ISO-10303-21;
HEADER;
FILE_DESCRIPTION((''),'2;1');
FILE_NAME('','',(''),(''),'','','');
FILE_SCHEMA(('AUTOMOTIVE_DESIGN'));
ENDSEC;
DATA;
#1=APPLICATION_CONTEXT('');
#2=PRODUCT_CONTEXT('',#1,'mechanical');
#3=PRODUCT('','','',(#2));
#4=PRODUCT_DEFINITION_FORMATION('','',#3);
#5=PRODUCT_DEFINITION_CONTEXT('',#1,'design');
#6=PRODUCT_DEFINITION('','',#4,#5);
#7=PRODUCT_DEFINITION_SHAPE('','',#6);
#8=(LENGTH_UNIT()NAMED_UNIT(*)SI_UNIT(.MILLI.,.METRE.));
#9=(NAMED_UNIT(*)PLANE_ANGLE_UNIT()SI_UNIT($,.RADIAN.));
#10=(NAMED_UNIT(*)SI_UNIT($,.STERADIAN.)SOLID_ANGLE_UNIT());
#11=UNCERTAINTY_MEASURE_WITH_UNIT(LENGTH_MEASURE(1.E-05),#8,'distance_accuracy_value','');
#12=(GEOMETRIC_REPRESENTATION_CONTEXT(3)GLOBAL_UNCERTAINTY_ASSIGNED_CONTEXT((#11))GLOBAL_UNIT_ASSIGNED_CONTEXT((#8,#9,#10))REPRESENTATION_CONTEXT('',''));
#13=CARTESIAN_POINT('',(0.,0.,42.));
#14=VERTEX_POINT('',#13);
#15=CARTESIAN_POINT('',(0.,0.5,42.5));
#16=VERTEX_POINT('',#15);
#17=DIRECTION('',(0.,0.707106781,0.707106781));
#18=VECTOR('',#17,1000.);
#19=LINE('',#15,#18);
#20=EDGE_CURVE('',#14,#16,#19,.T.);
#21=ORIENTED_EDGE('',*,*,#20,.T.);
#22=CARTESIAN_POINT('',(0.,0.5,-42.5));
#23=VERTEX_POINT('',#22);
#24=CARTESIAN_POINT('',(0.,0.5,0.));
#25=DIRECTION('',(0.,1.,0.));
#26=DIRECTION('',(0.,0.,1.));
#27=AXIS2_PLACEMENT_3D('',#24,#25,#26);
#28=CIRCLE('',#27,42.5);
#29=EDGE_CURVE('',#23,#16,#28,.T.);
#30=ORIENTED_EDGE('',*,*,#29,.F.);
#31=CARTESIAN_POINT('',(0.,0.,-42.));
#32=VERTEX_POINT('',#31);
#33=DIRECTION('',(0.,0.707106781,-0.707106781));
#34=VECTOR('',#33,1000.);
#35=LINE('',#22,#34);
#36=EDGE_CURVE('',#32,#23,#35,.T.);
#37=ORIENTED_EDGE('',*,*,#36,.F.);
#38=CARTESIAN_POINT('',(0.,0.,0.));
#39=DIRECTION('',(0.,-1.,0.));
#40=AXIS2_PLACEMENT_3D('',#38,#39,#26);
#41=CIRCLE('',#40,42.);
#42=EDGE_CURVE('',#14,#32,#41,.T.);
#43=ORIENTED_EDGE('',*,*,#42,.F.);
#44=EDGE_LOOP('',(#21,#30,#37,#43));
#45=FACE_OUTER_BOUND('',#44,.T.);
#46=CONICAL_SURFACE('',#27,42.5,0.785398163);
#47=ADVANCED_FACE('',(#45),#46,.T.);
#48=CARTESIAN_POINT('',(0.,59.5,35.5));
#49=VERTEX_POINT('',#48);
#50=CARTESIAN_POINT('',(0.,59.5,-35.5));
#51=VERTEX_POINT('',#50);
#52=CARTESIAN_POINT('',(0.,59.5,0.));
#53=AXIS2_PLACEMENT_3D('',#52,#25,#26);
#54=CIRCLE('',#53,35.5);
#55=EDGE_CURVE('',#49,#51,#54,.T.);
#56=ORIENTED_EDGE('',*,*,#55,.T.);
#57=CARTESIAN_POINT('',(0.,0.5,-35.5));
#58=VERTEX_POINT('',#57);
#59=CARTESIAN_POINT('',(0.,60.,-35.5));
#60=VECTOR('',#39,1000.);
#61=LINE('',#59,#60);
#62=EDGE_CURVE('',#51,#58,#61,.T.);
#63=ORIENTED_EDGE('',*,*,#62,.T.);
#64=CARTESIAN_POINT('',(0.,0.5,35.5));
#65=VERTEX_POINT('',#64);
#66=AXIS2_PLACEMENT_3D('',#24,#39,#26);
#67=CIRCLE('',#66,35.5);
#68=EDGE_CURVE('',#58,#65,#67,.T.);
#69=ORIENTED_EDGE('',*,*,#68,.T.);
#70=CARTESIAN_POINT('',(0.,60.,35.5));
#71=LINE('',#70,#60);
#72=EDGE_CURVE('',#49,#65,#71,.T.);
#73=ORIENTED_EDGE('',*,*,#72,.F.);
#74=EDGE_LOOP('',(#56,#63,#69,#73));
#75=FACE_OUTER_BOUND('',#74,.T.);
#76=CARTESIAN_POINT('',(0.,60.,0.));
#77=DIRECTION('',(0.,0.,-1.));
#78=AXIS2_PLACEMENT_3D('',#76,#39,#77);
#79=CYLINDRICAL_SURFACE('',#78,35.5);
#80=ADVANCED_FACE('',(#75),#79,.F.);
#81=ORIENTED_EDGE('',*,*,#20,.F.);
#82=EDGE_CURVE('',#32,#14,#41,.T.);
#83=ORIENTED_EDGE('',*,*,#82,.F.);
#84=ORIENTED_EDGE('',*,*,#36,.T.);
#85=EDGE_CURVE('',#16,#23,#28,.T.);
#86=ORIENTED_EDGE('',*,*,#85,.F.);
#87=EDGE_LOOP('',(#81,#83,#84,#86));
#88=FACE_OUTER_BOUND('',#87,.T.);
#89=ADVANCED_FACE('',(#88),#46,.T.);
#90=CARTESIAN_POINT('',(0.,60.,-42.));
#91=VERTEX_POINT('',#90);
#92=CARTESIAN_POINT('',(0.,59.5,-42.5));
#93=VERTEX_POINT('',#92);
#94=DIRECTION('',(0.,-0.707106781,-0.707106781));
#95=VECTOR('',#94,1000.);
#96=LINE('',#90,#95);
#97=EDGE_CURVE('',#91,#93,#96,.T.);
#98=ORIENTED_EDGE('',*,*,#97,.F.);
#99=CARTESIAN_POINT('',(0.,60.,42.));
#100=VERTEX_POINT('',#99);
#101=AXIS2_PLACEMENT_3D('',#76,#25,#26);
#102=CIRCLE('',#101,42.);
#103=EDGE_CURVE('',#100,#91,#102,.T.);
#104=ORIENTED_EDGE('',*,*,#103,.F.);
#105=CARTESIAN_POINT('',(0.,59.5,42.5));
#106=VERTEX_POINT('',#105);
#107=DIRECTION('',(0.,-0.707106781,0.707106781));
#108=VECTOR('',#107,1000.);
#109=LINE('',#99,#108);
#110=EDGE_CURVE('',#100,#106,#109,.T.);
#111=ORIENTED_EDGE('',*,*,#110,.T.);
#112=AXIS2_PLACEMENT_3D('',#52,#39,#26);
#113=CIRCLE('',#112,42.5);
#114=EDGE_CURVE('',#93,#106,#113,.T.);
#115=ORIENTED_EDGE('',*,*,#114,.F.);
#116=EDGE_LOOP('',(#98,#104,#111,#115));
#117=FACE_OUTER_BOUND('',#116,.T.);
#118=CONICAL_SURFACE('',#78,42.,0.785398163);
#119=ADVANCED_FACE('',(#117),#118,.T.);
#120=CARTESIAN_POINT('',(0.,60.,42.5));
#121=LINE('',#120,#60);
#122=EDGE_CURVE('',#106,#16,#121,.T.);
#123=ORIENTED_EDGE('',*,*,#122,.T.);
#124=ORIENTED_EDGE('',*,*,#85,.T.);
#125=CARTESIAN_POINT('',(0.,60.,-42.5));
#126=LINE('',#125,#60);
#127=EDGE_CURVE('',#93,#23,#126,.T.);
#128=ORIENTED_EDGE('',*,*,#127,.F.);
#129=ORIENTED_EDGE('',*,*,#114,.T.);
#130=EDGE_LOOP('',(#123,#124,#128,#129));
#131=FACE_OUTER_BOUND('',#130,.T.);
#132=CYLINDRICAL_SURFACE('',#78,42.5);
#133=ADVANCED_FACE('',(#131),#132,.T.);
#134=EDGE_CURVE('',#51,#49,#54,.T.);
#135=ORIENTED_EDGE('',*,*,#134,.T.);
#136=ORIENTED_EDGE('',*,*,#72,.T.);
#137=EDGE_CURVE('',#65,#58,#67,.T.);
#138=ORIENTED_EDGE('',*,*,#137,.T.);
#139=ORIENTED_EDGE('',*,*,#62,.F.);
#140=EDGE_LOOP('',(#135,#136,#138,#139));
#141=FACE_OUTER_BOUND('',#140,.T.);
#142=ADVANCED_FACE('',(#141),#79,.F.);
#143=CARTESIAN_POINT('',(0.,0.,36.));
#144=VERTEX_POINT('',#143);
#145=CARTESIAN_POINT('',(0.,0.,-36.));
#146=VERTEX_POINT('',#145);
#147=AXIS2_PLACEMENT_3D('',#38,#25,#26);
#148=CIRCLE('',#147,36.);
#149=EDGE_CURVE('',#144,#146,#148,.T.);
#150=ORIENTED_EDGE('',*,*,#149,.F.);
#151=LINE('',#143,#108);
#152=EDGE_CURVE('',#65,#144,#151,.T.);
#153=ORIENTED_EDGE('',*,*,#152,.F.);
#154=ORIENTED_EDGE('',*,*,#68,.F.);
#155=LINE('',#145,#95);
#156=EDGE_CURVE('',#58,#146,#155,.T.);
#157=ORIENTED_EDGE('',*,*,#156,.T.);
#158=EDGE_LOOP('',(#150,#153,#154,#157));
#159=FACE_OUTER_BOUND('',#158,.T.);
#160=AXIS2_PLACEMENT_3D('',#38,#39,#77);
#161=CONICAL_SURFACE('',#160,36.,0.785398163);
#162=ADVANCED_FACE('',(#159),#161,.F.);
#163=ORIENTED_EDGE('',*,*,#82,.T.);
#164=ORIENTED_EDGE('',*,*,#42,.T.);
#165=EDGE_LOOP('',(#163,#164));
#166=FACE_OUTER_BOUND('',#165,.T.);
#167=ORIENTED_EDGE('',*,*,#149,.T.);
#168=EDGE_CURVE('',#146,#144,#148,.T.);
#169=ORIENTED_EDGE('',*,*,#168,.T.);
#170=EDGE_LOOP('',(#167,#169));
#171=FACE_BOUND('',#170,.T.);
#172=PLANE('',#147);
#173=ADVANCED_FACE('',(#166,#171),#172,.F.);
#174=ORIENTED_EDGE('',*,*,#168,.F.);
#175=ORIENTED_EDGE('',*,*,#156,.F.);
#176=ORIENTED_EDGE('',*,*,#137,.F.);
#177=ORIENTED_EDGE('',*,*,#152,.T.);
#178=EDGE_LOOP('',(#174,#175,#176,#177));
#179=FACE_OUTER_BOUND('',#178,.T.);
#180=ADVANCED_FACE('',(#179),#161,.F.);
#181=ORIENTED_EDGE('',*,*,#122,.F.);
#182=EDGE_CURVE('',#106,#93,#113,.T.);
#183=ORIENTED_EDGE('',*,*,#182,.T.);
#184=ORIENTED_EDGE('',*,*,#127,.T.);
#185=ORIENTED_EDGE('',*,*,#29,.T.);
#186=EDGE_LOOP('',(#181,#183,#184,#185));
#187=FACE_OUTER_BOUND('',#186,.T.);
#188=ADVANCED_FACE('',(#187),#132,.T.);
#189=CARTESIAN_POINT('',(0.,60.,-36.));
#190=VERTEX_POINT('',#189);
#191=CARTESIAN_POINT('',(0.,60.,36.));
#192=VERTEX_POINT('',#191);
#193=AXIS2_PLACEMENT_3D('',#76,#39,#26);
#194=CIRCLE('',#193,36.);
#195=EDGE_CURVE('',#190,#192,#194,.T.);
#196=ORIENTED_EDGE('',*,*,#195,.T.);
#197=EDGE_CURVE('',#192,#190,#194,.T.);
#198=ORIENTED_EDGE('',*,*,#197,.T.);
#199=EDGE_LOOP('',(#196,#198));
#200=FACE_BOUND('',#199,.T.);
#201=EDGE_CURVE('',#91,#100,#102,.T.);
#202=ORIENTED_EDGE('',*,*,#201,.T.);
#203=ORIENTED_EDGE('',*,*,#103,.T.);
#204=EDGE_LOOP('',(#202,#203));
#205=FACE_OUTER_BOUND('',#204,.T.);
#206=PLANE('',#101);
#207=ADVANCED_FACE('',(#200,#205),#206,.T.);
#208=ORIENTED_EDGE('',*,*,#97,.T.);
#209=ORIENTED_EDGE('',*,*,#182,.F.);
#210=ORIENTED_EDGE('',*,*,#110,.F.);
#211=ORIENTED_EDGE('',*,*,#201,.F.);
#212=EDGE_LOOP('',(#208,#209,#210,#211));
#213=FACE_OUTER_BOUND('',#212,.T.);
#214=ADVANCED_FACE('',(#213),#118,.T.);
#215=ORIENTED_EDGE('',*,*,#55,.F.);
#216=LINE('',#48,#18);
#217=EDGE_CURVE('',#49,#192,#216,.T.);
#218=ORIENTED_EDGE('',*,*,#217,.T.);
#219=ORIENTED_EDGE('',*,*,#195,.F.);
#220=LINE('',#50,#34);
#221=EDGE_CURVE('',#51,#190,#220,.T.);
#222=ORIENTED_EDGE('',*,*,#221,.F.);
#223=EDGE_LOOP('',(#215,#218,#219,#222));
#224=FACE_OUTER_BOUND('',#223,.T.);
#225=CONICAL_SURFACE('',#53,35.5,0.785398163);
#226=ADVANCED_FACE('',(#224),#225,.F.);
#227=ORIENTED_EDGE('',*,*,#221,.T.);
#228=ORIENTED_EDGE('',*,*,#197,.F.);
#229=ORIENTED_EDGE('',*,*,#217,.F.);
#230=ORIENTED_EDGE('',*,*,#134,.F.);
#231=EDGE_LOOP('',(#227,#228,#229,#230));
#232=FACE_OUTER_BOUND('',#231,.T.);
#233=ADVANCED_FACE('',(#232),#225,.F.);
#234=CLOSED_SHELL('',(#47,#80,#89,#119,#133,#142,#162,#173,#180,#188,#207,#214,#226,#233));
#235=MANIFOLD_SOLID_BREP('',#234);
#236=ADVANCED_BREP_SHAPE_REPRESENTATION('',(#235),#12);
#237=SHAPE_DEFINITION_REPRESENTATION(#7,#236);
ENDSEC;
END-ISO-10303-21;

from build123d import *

# Parameters (mm, degrees)
SKETCH1_R           = 42.5
SKETCH1_R_2         = 35.5
BOSS_EXTRUDE1_DEPTH = 60
CHAMFER1_SIZE       = 0.5


with BuildPart() as part:
    # Sketch1 → Boss-Extrude1 (new body)
    with BuildSketch(Plane(origin=(0, 0, 0), x_dir=(1, 0, 0), z_dir=(0, 1, 0))):
        with Locations(Location((0, 0, 0), (0, 0, 270))):
            Circle(SKETCH1_R)
        with Locations(Location((0, 0, 0), (0, 0, 270))):
            Circle(SKETCH1_R_2, mode=Mode.SUBTRACT)
    extrude(amount=BOSS_EXTRUDE1_DEPTH)

    # Chamfer1
    chamfer1_edges = [part.edges().sort_by_distance(p)[0] for p in [
        (0, 0, -42.5),
        (0, 60, -42.5),
        (0, 0, -35.5),
        (0, 60, -35.5),
    ]]
    chamfer(chamfer1_edges, length=CHAMFER1_SIZE)


solid = part.part
